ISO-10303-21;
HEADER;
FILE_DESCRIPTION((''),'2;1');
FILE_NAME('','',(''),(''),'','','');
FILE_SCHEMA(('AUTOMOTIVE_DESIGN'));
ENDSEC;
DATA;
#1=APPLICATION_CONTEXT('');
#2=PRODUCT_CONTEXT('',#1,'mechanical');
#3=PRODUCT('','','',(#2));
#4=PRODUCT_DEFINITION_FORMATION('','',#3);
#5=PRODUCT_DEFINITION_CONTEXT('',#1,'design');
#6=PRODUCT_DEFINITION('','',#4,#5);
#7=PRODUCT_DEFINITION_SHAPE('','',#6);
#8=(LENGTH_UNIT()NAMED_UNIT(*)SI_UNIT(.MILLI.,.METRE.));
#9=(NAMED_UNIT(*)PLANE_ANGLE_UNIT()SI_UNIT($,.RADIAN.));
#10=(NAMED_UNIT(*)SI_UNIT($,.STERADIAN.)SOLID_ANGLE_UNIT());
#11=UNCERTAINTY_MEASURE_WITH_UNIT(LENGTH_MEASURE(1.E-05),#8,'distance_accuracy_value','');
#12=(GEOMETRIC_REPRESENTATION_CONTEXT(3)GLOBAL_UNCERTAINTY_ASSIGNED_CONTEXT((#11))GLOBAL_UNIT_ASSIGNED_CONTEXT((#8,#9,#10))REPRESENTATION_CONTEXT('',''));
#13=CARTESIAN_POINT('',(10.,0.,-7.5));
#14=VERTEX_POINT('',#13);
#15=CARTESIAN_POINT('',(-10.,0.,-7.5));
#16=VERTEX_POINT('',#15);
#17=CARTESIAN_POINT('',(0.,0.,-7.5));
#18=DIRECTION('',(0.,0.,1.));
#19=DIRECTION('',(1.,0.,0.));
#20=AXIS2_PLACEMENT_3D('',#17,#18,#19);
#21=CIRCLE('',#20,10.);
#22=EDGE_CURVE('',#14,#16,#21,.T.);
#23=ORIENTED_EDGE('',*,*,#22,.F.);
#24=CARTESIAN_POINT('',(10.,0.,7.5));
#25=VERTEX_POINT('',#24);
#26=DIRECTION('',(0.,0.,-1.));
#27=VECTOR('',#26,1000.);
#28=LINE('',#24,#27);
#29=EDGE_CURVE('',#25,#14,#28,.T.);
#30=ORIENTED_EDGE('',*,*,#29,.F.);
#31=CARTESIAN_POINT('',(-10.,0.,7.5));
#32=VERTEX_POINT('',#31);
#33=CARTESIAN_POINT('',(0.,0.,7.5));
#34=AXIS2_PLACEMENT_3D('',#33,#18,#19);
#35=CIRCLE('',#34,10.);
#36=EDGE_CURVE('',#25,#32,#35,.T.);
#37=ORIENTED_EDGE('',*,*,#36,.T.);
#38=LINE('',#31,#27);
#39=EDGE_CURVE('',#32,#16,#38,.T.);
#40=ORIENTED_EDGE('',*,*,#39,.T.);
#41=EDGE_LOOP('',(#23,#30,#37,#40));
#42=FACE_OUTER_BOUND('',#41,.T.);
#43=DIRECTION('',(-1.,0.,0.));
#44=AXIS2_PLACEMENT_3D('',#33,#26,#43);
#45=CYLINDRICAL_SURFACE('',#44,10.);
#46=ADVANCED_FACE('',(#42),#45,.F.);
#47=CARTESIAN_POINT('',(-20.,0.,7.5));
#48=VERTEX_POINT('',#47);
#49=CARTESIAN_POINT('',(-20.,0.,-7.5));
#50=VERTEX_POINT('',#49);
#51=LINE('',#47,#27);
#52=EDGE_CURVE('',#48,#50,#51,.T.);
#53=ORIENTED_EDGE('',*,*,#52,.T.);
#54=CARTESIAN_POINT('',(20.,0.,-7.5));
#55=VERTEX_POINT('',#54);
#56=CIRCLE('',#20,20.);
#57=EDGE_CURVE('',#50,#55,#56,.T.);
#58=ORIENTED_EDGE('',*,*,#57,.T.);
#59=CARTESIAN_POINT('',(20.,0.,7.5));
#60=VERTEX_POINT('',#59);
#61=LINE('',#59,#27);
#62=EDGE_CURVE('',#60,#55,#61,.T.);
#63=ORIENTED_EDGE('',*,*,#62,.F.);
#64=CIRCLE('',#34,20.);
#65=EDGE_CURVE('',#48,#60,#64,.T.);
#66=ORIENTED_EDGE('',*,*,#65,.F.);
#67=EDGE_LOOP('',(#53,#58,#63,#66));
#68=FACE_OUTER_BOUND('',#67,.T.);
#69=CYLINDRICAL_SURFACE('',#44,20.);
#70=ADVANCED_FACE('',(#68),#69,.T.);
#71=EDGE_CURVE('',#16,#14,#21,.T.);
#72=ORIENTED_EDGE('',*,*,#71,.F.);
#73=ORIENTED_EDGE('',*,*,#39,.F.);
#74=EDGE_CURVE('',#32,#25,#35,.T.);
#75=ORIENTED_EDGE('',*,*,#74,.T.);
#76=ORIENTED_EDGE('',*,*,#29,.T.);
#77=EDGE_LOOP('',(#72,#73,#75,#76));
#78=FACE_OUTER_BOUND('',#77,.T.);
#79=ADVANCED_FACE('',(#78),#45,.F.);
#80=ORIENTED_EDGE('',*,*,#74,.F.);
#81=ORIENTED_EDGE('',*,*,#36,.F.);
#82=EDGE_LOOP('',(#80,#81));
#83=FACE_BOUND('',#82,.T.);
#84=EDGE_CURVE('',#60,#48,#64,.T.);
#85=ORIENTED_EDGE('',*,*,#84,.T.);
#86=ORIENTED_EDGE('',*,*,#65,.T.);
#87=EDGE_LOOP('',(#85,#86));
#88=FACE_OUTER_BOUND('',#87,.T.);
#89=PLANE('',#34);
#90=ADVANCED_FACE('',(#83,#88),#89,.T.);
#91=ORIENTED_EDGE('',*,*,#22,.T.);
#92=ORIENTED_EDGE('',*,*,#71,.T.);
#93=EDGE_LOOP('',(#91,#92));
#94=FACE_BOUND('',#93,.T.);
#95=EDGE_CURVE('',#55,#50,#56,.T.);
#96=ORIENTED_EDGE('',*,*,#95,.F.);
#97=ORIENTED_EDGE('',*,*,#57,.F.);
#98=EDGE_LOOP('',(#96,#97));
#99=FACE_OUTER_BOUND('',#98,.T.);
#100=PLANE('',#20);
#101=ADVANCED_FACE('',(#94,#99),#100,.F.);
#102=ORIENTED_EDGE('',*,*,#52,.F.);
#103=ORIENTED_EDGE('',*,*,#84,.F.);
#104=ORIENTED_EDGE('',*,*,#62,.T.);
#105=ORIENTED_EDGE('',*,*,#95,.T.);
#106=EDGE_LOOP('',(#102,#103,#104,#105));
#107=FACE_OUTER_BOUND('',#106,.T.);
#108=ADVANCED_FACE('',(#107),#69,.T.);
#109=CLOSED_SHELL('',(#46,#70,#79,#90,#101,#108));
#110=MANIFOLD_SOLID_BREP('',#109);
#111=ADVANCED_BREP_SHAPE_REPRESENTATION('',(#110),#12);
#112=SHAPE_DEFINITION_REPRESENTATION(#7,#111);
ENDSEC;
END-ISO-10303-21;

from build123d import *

# Parameters (mm, degrees)
SKETCH_1_R      = 20
SKETCH_1_R_2    = 10
EXTRUDE_1_DEPTH = 7.5


with BuildPart() as part:
    # 草图1 → 凸台-拉伸1 (new, symmetric)
    with BuildSketch(Plane.XY):
        Circle(SKETCH_1_R)
        Circle(SKETCH_1_R_2, mode=Mode.SUBTRACT)
    extrude(amount=EXTRUDE_1_DEPTH, both=True)


solid = part.part
